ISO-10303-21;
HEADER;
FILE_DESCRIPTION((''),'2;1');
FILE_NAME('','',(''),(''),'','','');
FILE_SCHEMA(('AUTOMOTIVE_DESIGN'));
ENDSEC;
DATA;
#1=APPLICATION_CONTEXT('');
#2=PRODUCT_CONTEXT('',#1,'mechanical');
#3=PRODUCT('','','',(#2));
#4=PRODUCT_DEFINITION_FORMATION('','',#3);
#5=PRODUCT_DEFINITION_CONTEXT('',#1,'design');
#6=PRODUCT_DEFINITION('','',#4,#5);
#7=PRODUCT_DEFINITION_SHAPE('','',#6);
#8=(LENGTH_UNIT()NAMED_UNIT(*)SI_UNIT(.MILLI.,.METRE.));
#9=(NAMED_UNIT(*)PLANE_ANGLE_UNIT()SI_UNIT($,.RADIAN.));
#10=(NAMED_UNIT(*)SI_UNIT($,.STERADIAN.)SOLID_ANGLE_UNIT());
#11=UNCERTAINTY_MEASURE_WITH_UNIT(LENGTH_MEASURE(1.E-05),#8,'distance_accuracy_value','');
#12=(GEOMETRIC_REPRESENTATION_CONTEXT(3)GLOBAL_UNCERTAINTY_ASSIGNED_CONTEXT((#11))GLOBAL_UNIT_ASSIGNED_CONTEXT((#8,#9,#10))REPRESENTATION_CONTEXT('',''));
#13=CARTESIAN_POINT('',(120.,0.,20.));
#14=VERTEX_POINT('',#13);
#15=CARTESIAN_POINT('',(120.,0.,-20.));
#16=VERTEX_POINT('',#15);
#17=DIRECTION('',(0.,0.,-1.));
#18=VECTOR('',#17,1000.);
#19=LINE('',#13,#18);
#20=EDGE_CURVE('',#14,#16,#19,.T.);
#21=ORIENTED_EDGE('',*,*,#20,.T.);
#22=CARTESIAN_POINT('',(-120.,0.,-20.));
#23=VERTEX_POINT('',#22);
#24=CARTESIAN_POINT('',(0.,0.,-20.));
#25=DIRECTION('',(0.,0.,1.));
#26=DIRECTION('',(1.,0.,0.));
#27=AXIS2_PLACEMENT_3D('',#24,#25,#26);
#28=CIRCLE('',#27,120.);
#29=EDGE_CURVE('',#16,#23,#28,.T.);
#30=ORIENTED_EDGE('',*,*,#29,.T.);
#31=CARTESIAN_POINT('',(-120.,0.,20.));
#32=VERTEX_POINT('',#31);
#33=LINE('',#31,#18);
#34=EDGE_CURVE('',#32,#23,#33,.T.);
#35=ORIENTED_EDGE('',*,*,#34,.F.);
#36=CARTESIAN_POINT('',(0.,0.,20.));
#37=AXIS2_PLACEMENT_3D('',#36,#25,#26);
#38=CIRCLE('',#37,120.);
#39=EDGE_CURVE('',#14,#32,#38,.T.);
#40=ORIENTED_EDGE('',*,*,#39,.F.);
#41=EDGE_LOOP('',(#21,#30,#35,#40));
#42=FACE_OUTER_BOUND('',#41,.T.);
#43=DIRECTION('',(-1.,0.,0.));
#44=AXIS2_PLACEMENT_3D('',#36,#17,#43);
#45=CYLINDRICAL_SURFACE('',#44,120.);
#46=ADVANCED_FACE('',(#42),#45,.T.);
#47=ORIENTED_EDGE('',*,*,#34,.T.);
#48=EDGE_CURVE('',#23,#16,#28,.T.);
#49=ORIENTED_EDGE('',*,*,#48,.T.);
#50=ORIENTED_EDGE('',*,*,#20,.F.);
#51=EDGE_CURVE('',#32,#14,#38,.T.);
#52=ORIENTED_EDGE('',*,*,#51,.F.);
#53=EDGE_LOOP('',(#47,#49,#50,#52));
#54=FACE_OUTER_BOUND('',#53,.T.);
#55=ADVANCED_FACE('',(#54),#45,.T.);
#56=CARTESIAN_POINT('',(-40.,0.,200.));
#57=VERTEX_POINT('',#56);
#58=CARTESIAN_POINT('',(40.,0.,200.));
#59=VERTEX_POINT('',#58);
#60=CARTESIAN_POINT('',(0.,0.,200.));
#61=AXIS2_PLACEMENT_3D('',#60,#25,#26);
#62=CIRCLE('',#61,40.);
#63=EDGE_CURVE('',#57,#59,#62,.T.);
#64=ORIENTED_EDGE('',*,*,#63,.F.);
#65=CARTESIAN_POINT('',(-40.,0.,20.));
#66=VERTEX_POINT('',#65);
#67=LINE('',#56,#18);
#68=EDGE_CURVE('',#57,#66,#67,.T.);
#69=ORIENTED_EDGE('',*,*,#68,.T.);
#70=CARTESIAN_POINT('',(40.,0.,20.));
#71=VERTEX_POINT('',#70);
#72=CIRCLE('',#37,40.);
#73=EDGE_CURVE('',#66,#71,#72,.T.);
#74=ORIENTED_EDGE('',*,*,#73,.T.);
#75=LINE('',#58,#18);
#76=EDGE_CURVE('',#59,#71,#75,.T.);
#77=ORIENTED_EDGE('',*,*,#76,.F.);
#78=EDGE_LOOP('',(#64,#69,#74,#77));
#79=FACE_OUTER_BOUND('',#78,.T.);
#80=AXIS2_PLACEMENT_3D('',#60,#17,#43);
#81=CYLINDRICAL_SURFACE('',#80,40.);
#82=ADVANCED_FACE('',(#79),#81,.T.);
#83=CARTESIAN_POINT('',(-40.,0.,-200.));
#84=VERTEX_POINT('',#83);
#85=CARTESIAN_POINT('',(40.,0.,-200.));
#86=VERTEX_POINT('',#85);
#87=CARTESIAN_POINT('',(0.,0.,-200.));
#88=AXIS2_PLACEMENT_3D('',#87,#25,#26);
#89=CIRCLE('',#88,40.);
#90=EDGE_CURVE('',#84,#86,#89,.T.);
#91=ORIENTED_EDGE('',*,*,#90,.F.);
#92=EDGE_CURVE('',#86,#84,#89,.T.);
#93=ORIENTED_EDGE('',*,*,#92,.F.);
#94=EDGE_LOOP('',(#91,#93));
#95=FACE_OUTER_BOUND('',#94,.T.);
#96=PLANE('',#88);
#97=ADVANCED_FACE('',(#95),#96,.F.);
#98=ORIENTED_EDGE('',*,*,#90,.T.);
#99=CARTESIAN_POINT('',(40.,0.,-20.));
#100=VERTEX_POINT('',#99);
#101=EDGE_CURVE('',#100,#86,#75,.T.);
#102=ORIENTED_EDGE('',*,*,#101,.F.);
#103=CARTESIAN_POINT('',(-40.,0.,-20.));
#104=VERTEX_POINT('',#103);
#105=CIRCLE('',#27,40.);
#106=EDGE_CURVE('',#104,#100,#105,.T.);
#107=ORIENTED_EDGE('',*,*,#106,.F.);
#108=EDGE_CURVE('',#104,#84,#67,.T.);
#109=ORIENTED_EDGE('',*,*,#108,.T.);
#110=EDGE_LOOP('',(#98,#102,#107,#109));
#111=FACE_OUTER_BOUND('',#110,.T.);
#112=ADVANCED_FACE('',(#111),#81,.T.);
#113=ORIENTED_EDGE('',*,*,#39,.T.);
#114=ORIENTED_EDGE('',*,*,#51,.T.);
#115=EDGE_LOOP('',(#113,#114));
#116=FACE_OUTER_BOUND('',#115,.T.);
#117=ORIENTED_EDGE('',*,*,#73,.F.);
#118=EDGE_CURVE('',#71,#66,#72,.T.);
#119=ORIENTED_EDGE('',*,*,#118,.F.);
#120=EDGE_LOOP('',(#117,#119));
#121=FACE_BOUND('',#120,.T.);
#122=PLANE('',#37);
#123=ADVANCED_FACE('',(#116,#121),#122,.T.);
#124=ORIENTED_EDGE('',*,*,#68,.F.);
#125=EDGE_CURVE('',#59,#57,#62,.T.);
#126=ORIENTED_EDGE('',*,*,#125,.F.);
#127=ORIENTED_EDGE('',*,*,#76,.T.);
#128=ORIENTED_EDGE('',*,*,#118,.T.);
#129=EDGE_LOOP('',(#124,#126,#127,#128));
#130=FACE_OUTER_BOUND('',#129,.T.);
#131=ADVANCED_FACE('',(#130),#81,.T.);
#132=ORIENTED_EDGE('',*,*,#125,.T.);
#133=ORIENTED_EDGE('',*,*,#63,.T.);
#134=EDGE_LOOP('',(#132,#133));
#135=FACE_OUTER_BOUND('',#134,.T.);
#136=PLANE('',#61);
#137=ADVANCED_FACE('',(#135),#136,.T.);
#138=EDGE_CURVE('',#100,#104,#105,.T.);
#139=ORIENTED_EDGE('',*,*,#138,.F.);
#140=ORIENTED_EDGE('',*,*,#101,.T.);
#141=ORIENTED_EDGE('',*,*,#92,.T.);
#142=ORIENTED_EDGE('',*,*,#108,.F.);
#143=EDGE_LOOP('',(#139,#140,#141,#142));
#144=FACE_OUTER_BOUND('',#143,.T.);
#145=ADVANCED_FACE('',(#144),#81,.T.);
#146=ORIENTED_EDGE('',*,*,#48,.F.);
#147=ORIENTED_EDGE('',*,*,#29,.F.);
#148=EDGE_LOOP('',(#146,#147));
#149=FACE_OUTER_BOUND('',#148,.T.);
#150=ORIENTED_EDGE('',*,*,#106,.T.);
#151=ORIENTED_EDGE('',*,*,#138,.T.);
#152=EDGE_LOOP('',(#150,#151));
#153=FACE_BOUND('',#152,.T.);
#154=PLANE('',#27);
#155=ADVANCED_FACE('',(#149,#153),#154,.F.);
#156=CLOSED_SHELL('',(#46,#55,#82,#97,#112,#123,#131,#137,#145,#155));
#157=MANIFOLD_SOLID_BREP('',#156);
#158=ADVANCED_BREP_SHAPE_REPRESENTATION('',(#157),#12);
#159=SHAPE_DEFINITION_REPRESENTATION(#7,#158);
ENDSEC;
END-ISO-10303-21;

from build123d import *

# Parameters (mm, degrees)
SKETCH1_R           = 40
BOSS_EXTRUDE1_DEPTH = 200
SKETCH2_R           = 120
BOSS_EXTRUDE2_DEPTH = 20


with BuildPart() as part:
    # Sketch1 → Boss-Extrude1 (new, symmetric)
    with BuildSketch(Plane.XY):
        Circle(SKETCH1_R)
    extrude(amount=BOSS_EXTRUDE1_DEPTH, both=True)

    # Sketch2 → Boss-Extrude2 (add, symmetric)
    with BuildSketch(Plane.XY):
        Circle(SKETCH2_R)
    extrude(amount=BOSS_EXTRUDE2_DEPTH, both=True)


solid = part.part
